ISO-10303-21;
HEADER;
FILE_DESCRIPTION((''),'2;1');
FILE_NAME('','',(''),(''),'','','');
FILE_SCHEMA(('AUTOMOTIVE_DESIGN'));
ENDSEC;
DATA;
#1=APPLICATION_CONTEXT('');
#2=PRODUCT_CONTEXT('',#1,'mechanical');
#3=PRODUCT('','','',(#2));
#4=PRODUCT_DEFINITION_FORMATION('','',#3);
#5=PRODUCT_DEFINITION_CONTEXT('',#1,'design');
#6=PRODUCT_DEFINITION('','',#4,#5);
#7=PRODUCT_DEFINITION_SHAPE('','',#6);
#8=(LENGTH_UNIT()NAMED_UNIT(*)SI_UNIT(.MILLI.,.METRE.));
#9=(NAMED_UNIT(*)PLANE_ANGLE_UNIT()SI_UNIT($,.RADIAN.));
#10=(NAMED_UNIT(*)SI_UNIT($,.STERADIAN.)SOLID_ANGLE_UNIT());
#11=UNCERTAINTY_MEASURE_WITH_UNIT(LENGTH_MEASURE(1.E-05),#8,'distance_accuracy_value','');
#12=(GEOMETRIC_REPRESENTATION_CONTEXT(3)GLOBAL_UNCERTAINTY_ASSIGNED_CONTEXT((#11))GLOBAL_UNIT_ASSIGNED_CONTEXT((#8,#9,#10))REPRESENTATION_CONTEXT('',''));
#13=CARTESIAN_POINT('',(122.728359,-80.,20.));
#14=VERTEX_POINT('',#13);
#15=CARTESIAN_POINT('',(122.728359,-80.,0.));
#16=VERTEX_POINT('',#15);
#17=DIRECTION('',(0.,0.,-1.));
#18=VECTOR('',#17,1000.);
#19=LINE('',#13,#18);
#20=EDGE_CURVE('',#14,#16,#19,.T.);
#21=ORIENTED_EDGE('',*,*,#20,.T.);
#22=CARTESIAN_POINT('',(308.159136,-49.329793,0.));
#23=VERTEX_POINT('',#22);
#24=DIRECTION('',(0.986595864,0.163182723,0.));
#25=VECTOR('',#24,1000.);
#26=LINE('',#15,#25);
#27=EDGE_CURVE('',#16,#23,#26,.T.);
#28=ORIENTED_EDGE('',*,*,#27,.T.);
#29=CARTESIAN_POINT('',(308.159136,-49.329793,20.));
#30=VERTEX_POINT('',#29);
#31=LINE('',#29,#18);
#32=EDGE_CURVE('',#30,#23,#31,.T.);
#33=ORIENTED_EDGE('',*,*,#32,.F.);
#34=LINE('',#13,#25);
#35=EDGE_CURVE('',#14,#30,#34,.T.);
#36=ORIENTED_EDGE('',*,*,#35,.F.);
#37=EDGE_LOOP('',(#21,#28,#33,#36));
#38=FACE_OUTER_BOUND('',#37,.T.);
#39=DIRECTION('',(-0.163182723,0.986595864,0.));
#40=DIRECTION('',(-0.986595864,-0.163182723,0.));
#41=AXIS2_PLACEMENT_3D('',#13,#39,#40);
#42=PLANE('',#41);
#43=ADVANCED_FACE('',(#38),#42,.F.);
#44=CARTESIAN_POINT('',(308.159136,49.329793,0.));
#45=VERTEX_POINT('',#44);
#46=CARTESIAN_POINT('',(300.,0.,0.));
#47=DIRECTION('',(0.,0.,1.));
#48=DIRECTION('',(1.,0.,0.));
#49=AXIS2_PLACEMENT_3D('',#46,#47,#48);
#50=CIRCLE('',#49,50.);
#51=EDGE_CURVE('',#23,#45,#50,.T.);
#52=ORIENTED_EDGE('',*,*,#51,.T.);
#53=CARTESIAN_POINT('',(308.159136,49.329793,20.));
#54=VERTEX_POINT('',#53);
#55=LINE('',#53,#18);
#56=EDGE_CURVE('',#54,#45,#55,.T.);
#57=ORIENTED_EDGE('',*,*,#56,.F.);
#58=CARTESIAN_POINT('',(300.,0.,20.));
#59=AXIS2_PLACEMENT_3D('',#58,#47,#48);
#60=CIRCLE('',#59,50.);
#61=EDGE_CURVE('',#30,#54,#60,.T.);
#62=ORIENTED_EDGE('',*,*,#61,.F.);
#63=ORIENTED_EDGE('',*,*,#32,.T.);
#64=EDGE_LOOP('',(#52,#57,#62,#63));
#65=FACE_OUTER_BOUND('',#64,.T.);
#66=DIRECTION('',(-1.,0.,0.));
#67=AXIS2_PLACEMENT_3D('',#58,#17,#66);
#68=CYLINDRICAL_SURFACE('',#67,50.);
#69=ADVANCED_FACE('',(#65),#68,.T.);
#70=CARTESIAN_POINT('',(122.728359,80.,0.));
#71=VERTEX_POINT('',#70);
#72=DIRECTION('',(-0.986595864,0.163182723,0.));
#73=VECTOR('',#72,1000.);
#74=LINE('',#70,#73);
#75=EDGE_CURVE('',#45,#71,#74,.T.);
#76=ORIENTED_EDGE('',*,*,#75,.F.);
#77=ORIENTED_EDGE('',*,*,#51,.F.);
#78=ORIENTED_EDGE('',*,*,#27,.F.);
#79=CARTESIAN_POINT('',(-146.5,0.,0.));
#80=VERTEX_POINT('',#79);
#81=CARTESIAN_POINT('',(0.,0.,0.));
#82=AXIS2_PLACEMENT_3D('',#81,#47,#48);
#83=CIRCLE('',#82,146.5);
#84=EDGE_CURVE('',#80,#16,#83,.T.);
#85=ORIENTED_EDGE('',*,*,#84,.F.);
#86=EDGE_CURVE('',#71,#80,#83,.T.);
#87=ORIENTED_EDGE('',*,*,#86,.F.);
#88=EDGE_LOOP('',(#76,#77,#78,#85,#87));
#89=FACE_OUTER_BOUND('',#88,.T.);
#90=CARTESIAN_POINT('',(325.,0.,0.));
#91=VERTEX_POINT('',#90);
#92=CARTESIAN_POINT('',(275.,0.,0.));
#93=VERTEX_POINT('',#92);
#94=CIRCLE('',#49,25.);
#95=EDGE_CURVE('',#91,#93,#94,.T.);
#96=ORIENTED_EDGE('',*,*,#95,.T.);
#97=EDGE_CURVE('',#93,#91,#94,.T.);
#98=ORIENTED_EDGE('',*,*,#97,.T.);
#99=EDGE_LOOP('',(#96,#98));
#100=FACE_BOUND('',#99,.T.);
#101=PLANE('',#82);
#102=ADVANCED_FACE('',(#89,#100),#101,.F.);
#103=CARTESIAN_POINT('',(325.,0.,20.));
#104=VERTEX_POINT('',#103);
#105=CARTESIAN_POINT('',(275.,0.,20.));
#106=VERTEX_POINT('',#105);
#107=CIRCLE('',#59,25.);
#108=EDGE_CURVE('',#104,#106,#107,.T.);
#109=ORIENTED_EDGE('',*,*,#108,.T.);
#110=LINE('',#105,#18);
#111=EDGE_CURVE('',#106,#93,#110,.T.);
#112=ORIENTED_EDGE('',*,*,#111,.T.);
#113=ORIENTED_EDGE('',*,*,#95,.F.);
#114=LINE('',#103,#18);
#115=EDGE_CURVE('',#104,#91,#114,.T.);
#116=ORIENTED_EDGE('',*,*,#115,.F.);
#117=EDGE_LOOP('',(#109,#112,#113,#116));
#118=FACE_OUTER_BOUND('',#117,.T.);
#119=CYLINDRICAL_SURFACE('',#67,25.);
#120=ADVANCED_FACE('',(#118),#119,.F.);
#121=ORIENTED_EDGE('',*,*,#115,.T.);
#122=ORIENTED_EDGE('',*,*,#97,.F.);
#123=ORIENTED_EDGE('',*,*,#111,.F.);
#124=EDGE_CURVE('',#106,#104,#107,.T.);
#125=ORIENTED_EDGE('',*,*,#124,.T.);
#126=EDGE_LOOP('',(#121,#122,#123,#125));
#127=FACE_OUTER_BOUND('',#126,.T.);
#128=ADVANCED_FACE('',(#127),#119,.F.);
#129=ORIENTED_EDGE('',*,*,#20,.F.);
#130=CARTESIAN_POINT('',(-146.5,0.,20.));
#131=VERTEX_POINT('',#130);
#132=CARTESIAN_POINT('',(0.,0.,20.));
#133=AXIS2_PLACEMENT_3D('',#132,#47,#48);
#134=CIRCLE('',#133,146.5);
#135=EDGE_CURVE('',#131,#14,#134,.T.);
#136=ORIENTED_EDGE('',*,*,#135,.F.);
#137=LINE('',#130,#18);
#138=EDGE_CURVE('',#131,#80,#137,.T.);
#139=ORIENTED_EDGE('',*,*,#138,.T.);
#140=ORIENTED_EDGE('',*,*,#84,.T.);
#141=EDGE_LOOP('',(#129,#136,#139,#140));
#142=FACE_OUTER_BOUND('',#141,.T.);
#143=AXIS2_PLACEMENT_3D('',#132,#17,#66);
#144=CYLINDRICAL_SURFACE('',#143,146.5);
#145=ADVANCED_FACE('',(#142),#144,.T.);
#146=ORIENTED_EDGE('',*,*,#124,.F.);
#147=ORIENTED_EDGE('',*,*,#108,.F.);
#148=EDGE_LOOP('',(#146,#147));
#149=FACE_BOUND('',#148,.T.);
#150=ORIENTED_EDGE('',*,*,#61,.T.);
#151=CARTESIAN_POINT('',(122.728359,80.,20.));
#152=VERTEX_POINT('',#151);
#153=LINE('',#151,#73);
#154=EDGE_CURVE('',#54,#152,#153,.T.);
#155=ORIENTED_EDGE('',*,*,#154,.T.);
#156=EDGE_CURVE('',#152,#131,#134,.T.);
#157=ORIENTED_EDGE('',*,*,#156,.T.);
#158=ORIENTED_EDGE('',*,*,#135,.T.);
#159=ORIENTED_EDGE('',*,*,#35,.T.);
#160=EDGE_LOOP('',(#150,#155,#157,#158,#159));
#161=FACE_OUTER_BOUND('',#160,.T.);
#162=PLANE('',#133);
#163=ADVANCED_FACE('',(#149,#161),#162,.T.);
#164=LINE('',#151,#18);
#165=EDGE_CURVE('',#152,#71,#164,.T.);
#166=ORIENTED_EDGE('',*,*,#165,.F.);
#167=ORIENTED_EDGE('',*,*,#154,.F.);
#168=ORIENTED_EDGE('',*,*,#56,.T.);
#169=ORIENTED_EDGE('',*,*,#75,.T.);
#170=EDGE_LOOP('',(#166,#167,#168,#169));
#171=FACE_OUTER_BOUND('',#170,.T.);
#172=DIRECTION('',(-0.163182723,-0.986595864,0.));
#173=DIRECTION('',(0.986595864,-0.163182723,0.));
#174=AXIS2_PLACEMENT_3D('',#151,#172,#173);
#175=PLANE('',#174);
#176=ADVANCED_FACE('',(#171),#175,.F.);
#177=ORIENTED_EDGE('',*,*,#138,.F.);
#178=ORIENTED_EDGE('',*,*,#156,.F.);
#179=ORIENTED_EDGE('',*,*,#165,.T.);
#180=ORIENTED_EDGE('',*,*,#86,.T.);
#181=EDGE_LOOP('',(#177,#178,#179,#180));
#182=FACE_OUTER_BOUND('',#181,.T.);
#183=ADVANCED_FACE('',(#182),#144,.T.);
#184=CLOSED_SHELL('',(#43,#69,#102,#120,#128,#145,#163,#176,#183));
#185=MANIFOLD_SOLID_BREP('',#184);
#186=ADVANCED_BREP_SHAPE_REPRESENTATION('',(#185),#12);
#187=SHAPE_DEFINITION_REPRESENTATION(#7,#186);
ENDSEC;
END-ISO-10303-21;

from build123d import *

# Parameters (mm, degrees)
SKETCH1_R           = 25
BOSS_EXTRUDE1_DEPTH = 20


with BuildPart() as part:
    # Sketch1 → Boss-Extrude1 (new body)
    with BuildSketch(Plane.XY):
        with BuildLine():
            Line((122.728358581, 80), (308.159136141, 49.329793203))
            ThreePointArc((308.159136141, 49.329793203), (350, 0), (308.159136141, -49.329793203))
            Line((308.159136141, -49.329793203), (122.728358581, -80))
            ThreePointArc((122.728358581, -80), (-146.5, 0), (122.728358581, 80))
        make_face()
        with Locations((300, 0)):
            Circle(SKETCH1_R, mode=Mode.SUBTRACT)
    extrude(amount=BOSS_EXTRUDE1_DEPTH)


solid = part.part
